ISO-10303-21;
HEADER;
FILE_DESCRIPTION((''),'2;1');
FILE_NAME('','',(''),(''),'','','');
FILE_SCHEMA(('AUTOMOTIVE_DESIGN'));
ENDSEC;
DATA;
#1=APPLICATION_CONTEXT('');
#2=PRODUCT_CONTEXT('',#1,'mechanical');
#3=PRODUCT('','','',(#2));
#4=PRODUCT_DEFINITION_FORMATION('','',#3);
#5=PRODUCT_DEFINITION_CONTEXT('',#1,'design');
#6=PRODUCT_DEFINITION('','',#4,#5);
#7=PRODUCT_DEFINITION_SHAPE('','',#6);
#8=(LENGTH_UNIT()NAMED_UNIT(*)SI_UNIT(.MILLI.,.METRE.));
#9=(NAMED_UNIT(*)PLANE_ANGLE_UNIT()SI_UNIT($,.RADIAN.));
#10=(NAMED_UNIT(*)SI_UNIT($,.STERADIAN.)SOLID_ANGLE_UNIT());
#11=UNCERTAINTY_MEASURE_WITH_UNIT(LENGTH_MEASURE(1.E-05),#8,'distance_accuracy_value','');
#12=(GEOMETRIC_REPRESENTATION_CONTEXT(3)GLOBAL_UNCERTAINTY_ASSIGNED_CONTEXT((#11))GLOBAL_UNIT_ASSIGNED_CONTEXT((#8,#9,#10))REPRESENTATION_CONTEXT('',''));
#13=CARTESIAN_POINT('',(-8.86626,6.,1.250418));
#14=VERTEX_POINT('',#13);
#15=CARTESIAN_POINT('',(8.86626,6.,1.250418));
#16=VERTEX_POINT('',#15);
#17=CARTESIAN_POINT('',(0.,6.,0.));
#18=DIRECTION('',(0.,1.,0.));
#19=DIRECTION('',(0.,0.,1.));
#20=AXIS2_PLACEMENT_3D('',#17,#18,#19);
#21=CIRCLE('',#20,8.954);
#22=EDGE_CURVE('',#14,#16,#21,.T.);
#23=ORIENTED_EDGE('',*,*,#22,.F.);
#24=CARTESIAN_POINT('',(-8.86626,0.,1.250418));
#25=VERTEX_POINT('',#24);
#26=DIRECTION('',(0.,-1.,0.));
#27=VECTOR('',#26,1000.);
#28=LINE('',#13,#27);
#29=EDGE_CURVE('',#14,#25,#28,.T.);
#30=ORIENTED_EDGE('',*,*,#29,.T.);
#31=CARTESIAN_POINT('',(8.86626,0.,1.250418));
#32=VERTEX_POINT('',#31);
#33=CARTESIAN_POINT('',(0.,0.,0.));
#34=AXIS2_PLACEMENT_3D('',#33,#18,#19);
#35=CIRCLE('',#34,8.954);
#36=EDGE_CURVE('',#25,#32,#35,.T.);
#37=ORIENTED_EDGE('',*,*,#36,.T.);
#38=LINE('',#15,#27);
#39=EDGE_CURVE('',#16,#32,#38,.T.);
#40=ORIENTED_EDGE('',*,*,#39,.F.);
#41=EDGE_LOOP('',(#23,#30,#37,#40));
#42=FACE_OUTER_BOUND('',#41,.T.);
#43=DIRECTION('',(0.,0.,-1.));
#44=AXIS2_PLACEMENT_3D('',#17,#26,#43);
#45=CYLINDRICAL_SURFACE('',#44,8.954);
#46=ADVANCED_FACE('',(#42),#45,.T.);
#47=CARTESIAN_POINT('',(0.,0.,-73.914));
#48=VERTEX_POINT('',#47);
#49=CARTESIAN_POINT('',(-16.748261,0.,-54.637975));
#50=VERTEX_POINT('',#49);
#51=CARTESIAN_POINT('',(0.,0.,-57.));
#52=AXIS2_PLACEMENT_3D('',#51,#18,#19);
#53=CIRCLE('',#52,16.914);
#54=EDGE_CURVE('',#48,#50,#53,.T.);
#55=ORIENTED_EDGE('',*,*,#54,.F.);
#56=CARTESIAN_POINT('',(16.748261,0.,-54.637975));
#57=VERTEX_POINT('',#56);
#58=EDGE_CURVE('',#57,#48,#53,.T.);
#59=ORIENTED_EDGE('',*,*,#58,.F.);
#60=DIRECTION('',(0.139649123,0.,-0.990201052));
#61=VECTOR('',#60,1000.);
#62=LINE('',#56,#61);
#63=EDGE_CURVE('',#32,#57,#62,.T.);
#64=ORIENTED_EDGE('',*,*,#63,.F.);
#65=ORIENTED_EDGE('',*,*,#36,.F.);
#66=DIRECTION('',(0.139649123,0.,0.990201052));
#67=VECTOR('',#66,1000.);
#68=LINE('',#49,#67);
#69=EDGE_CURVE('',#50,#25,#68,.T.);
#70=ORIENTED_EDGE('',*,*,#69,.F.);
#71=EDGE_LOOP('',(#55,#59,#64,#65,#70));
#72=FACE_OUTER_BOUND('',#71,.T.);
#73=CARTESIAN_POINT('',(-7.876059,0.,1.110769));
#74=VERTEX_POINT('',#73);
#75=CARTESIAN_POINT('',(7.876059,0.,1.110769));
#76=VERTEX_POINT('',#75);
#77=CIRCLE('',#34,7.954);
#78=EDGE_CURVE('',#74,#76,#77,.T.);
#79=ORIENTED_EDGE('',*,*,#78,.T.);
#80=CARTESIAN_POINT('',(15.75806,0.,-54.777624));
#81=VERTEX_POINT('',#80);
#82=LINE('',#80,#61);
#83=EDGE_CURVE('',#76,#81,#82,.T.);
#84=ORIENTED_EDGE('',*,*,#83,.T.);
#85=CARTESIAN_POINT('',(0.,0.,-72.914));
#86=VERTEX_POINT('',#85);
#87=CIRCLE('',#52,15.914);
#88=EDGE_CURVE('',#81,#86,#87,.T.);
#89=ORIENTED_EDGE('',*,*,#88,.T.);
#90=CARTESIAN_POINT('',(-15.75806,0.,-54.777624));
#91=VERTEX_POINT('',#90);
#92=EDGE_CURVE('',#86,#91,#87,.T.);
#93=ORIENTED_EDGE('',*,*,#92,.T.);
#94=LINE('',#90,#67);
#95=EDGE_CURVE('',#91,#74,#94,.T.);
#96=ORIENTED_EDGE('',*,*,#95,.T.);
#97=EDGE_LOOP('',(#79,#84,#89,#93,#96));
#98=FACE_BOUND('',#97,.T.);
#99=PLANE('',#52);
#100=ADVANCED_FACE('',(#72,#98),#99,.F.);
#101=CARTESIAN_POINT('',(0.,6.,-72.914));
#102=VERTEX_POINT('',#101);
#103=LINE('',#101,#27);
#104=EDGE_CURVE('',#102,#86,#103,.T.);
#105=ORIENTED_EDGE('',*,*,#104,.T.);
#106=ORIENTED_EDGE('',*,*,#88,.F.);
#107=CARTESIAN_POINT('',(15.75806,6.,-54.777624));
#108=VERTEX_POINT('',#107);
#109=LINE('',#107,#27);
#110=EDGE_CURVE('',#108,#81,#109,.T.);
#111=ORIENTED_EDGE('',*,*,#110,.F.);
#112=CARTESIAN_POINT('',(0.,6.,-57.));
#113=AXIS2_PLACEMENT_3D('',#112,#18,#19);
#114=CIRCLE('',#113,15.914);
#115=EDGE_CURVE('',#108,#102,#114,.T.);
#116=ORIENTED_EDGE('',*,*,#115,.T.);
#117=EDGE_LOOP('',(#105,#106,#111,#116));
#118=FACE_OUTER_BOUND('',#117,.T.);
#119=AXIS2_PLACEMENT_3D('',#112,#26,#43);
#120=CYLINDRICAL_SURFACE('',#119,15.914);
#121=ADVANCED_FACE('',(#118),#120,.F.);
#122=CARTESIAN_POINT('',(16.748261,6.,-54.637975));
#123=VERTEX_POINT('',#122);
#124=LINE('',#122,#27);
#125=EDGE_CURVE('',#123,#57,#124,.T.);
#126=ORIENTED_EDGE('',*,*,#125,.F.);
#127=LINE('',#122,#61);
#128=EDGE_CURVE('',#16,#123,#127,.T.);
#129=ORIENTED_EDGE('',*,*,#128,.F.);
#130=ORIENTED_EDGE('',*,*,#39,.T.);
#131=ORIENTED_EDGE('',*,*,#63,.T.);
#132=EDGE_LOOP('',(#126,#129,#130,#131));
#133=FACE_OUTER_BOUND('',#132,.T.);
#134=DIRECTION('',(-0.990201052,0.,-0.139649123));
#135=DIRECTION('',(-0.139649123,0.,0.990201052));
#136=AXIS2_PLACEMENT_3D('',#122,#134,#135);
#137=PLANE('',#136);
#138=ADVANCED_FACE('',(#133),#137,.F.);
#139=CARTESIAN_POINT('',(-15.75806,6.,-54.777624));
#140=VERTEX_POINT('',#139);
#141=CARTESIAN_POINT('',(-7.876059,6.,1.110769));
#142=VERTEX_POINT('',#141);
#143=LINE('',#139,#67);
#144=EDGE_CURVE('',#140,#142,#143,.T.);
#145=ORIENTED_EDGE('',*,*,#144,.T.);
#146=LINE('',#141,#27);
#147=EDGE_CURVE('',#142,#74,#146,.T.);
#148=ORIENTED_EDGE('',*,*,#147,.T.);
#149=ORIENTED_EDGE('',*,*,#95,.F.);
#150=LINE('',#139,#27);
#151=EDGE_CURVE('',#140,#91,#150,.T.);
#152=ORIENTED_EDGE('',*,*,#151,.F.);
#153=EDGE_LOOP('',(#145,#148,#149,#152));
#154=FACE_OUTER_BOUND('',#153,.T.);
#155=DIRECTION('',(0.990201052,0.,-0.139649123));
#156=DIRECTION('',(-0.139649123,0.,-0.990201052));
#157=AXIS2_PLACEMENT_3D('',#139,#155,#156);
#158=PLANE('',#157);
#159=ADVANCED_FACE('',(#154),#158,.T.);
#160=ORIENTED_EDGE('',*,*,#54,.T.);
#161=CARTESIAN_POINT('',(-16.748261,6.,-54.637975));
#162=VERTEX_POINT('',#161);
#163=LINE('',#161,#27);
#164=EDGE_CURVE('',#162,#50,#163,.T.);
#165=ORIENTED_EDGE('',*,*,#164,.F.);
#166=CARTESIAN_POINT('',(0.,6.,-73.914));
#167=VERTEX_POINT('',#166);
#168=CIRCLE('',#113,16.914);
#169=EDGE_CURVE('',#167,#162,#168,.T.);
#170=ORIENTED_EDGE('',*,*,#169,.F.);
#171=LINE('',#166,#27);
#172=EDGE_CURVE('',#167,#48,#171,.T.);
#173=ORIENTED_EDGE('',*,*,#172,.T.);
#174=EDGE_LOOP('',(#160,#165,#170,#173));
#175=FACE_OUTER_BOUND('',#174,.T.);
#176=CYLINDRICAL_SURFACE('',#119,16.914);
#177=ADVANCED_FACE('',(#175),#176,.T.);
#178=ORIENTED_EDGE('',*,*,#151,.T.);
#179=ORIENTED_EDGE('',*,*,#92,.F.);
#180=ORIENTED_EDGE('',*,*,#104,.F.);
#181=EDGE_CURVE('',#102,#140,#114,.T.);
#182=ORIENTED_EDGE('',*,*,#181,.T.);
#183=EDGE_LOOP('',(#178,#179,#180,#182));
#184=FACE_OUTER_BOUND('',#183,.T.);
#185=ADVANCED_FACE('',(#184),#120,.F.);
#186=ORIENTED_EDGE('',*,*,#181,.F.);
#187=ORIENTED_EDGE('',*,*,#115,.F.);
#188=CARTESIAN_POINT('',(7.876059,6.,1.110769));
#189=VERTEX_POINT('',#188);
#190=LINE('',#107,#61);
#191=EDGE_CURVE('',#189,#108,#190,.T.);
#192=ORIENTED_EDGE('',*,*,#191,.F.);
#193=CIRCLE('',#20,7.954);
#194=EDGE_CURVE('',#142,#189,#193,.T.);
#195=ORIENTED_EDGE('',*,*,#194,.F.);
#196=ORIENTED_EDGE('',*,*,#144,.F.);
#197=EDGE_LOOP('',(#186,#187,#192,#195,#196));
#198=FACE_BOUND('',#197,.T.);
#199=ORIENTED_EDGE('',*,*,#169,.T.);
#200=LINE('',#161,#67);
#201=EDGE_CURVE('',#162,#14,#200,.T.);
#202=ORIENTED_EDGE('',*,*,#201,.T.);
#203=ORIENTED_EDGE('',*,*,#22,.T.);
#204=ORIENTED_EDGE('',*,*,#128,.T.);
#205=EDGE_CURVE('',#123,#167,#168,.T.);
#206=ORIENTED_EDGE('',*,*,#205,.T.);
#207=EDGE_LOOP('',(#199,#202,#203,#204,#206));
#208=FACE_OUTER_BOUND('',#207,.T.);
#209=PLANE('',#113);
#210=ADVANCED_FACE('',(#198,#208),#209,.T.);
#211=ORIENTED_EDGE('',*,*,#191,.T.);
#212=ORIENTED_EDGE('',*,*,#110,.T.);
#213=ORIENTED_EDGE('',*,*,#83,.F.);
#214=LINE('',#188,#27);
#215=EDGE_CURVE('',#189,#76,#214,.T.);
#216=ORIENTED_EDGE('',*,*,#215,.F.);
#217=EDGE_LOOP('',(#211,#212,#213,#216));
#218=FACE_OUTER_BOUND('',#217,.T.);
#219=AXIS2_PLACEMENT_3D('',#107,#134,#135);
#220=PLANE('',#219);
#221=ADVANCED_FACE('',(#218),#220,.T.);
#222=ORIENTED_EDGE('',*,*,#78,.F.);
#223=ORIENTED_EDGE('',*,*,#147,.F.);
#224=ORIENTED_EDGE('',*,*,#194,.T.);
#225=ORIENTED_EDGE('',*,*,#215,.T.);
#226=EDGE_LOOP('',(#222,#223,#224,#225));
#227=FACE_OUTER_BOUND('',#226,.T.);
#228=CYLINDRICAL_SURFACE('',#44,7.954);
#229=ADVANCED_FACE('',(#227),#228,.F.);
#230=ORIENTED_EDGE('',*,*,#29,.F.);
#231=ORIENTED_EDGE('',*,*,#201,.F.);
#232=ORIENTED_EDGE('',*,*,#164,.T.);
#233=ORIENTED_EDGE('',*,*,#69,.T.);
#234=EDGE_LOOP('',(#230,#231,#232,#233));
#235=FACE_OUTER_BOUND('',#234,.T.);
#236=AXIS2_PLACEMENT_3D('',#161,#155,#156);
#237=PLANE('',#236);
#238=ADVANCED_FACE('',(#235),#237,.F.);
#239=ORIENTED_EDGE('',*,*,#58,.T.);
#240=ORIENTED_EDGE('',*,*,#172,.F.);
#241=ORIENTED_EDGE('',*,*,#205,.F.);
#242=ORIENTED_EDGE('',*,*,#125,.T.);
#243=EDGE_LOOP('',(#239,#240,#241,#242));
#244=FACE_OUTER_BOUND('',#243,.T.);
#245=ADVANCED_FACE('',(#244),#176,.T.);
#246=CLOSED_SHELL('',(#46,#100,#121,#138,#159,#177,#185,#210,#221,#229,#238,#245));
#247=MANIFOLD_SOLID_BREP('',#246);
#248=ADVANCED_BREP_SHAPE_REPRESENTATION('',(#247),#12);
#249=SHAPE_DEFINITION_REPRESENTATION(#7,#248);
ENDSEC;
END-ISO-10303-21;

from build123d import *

# Parameters (mm, degrees)
BOSS_EXTRUDE1_DEPTH = 6


with BuildPart() as part:
    # Sketch1 → Boss-Extrude1 (new body)
    with BuildSketch(Plane(origin=(0, 0, 0), x_dir=(1, 0, 0), z_dir=(0, 1, 0))):
        with BuildLine():
            Line((-16.748260586, 54.637974737), (-8.866260216, -1.250418246))
            ThreePointArc((-8.866260216, -1.250418246), (0, -8.954), (8.866260216, -1.250418246))
            Line((8.866260216, -1.250418246), (16.748260586, 54.637974737))
            ThreePointArc((16.748260586, 54.637974737), (0, 73.914), (-16.748260586, 54.637974737))
        make_face()
        with BuildLine():
            Line((-15.758059534, 54.77762386), (-7.876059164, -1.110769123))
            ThreePointArc((-7.876059164, -1.110769123), (0, -7.954), (7.876059164, -1.110769123))
            Line((7.876059164, -1.110769123), (15.758059534, 54.77762386))
            ThreePointArc((15.758059534, 54.77762386), (0, 72.914), (-15.758059534, 54.77762386))
        make_face(mode=Mode.SUBTRACT)
    extrude(amount=BOSS_EXTRUDE1_DEPTH)


solid = part.part
